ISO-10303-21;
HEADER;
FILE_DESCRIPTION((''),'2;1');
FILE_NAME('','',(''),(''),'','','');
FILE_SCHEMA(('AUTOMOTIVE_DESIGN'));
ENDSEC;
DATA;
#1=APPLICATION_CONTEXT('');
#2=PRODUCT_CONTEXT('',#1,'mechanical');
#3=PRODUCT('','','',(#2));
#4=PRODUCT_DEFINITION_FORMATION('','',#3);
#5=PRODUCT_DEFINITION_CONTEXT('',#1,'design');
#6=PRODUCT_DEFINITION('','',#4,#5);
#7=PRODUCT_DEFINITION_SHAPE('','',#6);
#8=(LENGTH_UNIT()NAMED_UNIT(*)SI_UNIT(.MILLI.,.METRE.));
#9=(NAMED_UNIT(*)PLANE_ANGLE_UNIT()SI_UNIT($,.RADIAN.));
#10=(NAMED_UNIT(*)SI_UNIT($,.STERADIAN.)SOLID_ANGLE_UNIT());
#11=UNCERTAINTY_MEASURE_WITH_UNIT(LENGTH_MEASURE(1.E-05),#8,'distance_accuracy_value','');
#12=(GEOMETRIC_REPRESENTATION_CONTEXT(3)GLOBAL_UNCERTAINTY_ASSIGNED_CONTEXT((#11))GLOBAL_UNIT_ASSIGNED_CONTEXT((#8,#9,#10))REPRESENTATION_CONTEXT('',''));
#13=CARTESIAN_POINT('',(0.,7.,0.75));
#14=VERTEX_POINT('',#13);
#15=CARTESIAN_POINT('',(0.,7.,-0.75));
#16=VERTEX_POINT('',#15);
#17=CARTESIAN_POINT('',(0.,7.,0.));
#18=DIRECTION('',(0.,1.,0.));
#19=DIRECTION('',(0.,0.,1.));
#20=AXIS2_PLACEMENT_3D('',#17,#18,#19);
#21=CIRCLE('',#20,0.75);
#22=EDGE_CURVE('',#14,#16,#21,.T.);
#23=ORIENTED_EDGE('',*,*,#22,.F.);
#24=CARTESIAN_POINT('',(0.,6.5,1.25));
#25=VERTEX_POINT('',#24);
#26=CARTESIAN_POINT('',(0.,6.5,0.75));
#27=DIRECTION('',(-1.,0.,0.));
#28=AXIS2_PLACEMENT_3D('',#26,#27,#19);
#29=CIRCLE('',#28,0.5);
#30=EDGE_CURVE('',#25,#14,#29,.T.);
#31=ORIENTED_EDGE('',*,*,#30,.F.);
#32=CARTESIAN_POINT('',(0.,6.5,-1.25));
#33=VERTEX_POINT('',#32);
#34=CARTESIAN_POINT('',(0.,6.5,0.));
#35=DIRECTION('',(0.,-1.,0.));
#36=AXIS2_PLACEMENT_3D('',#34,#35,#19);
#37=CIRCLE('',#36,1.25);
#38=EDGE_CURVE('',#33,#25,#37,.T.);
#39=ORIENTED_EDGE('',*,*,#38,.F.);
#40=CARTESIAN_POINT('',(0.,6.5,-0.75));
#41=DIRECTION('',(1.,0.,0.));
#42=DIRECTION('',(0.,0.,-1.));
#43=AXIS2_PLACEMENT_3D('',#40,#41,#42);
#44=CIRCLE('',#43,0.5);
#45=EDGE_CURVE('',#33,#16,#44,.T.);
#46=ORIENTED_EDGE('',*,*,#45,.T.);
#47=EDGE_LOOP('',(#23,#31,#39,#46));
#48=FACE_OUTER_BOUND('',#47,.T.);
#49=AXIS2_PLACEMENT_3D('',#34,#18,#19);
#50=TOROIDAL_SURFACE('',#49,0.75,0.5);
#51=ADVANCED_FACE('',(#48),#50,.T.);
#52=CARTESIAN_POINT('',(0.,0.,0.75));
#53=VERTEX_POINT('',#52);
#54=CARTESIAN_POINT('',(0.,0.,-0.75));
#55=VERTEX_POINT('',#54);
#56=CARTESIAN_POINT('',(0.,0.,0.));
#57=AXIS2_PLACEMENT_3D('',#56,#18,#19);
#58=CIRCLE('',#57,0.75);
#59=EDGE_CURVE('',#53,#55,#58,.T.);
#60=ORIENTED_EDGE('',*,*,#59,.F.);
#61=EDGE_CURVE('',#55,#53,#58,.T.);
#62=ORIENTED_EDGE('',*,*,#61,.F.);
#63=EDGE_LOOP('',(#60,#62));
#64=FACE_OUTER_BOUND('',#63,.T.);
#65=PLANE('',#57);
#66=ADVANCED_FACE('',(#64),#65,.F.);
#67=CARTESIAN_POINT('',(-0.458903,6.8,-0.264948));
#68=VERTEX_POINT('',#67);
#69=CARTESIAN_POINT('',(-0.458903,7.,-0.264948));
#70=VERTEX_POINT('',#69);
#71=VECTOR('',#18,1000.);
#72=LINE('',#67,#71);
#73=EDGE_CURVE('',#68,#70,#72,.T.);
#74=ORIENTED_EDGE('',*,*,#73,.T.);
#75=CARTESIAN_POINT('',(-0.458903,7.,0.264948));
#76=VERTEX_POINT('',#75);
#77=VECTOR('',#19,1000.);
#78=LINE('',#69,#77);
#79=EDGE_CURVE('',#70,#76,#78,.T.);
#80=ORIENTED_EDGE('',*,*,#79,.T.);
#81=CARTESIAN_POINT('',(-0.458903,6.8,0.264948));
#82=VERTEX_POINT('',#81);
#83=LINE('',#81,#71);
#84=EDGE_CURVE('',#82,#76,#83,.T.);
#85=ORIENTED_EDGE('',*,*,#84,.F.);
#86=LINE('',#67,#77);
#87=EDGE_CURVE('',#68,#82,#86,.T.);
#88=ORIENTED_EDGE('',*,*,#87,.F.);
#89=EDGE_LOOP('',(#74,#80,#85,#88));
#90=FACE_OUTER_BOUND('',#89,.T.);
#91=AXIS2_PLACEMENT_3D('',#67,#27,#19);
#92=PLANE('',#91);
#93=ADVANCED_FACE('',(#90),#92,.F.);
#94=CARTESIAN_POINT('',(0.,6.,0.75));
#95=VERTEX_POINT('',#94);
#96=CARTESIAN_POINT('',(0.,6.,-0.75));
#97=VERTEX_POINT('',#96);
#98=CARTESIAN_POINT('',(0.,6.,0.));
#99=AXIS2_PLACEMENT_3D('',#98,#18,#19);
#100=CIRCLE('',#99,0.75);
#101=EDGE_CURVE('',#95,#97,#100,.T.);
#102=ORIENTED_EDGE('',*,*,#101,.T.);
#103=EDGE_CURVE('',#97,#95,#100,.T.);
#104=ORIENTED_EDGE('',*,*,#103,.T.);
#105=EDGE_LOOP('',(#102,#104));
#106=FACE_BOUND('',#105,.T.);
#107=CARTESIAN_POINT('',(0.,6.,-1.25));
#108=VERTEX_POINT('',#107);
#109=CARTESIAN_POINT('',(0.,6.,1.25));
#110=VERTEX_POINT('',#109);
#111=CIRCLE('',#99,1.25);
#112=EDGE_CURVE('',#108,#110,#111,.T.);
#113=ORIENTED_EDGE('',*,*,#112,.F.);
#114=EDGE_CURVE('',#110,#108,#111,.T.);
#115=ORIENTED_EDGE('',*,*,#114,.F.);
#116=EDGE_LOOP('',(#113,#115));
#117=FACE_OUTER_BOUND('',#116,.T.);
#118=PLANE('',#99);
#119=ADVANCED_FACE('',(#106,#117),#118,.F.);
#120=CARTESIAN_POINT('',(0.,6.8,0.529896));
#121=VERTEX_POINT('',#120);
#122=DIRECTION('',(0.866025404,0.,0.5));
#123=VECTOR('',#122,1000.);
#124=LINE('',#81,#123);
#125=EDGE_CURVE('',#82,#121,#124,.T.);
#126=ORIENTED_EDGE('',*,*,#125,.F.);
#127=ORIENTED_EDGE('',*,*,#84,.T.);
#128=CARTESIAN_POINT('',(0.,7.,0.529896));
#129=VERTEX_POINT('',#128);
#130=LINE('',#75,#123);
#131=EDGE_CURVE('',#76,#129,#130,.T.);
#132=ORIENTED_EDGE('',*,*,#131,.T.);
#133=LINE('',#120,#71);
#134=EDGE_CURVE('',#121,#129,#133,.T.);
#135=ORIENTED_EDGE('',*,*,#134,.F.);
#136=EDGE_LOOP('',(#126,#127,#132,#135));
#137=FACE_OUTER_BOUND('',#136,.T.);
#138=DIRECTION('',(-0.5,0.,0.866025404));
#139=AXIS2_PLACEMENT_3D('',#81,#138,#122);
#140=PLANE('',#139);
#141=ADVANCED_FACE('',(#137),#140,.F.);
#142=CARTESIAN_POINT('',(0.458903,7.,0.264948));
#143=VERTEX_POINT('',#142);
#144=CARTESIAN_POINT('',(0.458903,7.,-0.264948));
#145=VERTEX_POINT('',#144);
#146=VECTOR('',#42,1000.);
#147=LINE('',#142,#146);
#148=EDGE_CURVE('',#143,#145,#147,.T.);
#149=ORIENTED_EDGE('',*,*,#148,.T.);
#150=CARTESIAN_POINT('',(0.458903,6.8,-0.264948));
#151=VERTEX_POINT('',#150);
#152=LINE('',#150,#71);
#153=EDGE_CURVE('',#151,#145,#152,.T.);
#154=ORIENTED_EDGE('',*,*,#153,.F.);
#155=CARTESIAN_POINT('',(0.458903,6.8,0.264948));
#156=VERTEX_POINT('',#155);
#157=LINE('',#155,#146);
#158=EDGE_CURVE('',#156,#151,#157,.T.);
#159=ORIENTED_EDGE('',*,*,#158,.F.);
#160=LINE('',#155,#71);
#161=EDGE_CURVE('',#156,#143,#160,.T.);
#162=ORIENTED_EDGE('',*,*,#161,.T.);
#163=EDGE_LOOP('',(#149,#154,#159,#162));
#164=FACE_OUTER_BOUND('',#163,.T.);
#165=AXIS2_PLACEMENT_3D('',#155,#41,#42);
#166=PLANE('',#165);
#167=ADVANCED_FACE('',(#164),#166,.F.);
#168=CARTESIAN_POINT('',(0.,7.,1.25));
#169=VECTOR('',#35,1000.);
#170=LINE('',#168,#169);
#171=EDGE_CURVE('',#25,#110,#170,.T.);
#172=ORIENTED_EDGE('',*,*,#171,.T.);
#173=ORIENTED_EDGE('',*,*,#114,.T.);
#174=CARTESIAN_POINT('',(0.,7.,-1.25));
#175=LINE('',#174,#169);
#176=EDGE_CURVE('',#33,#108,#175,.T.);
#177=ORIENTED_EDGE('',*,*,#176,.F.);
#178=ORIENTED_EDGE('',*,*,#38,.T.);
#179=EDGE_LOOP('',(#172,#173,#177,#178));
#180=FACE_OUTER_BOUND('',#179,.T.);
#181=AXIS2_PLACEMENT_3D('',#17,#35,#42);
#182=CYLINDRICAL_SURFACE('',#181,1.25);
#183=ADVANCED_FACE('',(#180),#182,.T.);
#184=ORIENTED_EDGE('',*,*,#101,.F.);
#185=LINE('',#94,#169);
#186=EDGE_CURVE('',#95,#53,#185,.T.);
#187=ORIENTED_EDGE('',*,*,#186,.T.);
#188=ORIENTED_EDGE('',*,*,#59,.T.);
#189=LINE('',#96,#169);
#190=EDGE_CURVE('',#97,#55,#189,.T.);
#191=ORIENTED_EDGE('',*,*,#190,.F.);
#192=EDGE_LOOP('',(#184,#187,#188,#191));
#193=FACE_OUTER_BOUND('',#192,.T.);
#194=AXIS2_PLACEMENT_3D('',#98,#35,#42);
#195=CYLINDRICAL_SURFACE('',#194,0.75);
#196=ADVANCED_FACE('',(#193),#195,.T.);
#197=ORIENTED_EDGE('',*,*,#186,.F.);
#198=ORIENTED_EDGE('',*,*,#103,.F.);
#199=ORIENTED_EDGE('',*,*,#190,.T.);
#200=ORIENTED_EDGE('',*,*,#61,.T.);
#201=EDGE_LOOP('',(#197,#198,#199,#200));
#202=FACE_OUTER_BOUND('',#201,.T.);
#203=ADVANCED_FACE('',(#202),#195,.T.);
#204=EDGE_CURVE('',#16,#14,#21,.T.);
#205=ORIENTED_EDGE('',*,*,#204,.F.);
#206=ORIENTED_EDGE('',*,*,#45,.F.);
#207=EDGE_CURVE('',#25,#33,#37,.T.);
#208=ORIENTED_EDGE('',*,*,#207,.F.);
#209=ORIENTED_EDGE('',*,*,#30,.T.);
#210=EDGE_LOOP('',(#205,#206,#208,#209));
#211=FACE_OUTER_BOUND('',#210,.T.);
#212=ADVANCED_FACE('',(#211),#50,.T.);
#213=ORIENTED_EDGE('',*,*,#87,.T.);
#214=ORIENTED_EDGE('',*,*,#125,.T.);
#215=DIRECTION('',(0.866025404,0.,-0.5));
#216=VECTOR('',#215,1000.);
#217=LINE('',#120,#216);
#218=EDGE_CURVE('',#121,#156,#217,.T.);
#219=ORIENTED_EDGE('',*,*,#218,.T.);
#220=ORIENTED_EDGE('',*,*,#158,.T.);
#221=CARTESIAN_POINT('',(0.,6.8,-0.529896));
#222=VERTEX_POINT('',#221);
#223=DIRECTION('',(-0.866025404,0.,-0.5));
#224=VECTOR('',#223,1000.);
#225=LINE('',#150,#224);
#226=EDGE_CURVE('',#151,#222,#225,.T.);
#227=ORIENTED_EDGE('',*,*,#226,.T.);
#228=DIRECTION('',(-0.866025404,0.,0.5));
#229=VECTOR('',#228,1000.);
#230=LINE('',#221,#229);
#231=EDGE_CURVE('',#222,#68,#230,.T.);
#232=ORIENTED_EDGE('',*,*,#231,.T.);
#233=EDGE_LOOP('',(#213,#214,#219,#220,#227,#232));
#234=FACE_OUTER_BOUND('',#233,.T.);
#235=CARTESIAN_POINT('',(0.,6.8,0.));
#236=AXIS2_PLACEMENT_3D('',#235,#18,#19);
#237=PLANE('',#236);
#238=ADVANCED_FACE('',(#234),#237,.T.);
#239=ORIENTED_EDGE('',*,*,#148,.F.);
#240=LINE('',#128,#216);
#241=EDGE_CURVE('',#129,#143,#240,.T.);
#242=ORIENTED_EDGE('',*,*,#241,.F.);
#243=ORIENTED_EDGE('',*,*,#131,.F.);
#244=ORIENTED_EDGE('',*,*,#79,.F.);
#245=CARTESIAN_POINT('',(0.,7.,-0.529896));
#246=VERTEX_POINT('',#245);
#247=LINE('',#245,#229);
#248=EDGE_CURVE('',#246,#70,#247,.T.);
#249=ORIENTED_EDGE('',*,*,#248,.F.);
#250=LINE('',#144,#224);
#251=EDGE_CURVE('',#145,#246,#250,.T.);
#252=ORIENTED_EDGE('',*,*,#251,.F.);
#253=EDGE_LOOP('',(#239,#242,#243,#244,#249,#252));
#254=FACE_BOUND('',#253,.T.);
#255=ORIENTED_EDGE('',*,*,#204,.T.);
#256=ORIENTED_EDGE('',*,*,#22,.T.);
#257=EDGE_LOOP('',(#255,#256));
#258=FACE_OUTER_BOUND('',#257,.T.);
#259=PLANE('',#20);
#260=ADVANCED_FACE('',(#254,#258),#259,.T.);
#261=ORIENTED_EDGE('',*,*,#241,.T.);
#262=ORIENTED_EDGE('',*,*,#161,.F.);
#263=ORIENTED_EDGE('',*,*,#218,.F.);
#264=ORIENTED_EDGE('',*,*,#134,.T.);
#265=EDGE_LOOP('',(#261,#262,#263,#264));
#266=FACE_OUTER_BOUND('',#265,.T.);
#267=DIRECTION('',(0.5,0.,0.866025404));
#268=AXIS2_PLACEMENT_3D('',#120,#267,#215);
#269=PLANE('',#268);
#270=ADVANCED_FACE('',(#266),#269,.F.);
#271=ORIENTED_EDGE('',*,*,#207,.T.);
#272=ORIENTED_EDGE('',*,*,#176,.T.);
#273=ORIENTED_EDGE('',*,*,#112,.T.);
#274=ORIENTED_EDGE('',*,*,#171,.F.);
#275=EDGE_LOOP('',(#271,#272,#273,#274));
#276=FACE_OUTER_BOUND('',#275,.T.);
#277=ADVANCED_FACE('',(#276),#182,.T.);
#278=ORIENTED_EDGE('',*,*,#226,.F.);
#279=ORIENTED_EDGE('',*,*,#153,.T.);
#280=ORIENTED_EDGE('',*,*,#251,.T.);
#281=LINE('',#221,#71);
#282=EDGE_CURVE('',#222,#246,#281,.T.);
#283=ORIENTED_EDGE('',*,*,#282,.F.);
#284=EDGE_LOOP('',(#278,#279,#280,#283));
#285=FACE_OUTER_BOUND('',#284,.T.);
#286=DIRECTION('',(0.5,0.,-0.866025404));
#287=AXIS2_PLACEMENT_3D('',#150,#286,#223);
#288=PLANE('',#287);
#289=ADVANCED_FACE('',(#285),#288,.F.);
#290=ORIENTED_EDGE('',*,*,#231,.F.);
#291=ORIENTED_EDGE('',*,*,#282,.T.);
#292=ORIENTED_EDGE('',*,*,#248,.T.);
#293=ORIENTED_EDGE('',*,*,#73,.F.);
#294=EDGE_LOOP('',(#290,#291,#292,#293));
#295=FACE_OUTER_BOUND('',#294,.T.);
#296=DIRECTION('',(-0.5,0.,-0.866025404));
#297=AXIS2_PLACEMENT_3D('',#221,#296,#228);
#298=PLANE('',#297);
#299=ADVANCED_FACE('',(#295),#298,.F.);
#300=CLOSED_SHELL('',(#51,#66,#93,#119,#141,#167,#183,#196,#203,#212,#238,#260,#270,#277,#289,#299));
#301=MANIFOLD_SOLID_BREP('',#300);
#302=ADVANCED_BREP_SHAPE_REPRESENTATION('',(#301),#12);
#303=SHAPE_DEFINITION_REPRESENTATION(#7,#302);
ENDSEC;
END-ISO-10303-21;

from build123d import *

# Parameters (mm, degrees)
SKETCH1_R           = 0.75
BOSS_EXTRUDE1_DEPTH = 6
SKETCH2_R           = 1.25
BOSS_EXTRUDE2_DEPTH = 1
FILLET1_R           = 0.5
CUT_EXTRUDE1_DEPTH  = 0.2


with BuildPart() as part:
    # Sketch1 → Boss-Extrude1 (new body)
    with BuildSketch(Plane(origin=(0, 0, 0), x_dir=(1, 0, 0), z_dir=(0, 1, 0))):
        with Locations(Location((0, 0, 0), (0, 0, 270))):
            Circle(SKETCH1_R)
    extrude(amount=BOSS_EXTRUDE1_DEPTH)

    # Sketch2 → Boss-Extrude2 (add)
    with BuildSketch(Plane(origin=(0, 6, 0), x_dir=(1, 0, 0), z_dir=(0, 1, 0))):
        with Locations(Location((0, 0, 0), (0, 0, 270))):
            Circle(SKETCH2_R)
    extrude(amount=BOSS_EXTRUDE2_DEPTH)

    # Fillet1
    fillet1_edges = [part.edges().sort_by_distance(p)[0] for p in [
        (0, 7, -1.25),
    ]]
    fillet(fillet1_edges, radius=FILLET1_R)

    # Sketch3 → Cut-Extrude1 (cut)
    with BuildSketch(Plane(origin=(0, 7, 0), x_dir=(1, 0, 0), z_dir=(0, 1, 0))):
        Polygon((0, 0.529895662), (-0.458903105, 0.264947831), (-0.458903105, -0.264947831), (0, -0.529895662), (0.458903105, -0.264947831), (0.458903105, 0.264947831), align=None)
    extrude(amount=-CUT_EXTRUDE1_DEPTH, mode=Mode.SUBTRACT)


solid = part.part
